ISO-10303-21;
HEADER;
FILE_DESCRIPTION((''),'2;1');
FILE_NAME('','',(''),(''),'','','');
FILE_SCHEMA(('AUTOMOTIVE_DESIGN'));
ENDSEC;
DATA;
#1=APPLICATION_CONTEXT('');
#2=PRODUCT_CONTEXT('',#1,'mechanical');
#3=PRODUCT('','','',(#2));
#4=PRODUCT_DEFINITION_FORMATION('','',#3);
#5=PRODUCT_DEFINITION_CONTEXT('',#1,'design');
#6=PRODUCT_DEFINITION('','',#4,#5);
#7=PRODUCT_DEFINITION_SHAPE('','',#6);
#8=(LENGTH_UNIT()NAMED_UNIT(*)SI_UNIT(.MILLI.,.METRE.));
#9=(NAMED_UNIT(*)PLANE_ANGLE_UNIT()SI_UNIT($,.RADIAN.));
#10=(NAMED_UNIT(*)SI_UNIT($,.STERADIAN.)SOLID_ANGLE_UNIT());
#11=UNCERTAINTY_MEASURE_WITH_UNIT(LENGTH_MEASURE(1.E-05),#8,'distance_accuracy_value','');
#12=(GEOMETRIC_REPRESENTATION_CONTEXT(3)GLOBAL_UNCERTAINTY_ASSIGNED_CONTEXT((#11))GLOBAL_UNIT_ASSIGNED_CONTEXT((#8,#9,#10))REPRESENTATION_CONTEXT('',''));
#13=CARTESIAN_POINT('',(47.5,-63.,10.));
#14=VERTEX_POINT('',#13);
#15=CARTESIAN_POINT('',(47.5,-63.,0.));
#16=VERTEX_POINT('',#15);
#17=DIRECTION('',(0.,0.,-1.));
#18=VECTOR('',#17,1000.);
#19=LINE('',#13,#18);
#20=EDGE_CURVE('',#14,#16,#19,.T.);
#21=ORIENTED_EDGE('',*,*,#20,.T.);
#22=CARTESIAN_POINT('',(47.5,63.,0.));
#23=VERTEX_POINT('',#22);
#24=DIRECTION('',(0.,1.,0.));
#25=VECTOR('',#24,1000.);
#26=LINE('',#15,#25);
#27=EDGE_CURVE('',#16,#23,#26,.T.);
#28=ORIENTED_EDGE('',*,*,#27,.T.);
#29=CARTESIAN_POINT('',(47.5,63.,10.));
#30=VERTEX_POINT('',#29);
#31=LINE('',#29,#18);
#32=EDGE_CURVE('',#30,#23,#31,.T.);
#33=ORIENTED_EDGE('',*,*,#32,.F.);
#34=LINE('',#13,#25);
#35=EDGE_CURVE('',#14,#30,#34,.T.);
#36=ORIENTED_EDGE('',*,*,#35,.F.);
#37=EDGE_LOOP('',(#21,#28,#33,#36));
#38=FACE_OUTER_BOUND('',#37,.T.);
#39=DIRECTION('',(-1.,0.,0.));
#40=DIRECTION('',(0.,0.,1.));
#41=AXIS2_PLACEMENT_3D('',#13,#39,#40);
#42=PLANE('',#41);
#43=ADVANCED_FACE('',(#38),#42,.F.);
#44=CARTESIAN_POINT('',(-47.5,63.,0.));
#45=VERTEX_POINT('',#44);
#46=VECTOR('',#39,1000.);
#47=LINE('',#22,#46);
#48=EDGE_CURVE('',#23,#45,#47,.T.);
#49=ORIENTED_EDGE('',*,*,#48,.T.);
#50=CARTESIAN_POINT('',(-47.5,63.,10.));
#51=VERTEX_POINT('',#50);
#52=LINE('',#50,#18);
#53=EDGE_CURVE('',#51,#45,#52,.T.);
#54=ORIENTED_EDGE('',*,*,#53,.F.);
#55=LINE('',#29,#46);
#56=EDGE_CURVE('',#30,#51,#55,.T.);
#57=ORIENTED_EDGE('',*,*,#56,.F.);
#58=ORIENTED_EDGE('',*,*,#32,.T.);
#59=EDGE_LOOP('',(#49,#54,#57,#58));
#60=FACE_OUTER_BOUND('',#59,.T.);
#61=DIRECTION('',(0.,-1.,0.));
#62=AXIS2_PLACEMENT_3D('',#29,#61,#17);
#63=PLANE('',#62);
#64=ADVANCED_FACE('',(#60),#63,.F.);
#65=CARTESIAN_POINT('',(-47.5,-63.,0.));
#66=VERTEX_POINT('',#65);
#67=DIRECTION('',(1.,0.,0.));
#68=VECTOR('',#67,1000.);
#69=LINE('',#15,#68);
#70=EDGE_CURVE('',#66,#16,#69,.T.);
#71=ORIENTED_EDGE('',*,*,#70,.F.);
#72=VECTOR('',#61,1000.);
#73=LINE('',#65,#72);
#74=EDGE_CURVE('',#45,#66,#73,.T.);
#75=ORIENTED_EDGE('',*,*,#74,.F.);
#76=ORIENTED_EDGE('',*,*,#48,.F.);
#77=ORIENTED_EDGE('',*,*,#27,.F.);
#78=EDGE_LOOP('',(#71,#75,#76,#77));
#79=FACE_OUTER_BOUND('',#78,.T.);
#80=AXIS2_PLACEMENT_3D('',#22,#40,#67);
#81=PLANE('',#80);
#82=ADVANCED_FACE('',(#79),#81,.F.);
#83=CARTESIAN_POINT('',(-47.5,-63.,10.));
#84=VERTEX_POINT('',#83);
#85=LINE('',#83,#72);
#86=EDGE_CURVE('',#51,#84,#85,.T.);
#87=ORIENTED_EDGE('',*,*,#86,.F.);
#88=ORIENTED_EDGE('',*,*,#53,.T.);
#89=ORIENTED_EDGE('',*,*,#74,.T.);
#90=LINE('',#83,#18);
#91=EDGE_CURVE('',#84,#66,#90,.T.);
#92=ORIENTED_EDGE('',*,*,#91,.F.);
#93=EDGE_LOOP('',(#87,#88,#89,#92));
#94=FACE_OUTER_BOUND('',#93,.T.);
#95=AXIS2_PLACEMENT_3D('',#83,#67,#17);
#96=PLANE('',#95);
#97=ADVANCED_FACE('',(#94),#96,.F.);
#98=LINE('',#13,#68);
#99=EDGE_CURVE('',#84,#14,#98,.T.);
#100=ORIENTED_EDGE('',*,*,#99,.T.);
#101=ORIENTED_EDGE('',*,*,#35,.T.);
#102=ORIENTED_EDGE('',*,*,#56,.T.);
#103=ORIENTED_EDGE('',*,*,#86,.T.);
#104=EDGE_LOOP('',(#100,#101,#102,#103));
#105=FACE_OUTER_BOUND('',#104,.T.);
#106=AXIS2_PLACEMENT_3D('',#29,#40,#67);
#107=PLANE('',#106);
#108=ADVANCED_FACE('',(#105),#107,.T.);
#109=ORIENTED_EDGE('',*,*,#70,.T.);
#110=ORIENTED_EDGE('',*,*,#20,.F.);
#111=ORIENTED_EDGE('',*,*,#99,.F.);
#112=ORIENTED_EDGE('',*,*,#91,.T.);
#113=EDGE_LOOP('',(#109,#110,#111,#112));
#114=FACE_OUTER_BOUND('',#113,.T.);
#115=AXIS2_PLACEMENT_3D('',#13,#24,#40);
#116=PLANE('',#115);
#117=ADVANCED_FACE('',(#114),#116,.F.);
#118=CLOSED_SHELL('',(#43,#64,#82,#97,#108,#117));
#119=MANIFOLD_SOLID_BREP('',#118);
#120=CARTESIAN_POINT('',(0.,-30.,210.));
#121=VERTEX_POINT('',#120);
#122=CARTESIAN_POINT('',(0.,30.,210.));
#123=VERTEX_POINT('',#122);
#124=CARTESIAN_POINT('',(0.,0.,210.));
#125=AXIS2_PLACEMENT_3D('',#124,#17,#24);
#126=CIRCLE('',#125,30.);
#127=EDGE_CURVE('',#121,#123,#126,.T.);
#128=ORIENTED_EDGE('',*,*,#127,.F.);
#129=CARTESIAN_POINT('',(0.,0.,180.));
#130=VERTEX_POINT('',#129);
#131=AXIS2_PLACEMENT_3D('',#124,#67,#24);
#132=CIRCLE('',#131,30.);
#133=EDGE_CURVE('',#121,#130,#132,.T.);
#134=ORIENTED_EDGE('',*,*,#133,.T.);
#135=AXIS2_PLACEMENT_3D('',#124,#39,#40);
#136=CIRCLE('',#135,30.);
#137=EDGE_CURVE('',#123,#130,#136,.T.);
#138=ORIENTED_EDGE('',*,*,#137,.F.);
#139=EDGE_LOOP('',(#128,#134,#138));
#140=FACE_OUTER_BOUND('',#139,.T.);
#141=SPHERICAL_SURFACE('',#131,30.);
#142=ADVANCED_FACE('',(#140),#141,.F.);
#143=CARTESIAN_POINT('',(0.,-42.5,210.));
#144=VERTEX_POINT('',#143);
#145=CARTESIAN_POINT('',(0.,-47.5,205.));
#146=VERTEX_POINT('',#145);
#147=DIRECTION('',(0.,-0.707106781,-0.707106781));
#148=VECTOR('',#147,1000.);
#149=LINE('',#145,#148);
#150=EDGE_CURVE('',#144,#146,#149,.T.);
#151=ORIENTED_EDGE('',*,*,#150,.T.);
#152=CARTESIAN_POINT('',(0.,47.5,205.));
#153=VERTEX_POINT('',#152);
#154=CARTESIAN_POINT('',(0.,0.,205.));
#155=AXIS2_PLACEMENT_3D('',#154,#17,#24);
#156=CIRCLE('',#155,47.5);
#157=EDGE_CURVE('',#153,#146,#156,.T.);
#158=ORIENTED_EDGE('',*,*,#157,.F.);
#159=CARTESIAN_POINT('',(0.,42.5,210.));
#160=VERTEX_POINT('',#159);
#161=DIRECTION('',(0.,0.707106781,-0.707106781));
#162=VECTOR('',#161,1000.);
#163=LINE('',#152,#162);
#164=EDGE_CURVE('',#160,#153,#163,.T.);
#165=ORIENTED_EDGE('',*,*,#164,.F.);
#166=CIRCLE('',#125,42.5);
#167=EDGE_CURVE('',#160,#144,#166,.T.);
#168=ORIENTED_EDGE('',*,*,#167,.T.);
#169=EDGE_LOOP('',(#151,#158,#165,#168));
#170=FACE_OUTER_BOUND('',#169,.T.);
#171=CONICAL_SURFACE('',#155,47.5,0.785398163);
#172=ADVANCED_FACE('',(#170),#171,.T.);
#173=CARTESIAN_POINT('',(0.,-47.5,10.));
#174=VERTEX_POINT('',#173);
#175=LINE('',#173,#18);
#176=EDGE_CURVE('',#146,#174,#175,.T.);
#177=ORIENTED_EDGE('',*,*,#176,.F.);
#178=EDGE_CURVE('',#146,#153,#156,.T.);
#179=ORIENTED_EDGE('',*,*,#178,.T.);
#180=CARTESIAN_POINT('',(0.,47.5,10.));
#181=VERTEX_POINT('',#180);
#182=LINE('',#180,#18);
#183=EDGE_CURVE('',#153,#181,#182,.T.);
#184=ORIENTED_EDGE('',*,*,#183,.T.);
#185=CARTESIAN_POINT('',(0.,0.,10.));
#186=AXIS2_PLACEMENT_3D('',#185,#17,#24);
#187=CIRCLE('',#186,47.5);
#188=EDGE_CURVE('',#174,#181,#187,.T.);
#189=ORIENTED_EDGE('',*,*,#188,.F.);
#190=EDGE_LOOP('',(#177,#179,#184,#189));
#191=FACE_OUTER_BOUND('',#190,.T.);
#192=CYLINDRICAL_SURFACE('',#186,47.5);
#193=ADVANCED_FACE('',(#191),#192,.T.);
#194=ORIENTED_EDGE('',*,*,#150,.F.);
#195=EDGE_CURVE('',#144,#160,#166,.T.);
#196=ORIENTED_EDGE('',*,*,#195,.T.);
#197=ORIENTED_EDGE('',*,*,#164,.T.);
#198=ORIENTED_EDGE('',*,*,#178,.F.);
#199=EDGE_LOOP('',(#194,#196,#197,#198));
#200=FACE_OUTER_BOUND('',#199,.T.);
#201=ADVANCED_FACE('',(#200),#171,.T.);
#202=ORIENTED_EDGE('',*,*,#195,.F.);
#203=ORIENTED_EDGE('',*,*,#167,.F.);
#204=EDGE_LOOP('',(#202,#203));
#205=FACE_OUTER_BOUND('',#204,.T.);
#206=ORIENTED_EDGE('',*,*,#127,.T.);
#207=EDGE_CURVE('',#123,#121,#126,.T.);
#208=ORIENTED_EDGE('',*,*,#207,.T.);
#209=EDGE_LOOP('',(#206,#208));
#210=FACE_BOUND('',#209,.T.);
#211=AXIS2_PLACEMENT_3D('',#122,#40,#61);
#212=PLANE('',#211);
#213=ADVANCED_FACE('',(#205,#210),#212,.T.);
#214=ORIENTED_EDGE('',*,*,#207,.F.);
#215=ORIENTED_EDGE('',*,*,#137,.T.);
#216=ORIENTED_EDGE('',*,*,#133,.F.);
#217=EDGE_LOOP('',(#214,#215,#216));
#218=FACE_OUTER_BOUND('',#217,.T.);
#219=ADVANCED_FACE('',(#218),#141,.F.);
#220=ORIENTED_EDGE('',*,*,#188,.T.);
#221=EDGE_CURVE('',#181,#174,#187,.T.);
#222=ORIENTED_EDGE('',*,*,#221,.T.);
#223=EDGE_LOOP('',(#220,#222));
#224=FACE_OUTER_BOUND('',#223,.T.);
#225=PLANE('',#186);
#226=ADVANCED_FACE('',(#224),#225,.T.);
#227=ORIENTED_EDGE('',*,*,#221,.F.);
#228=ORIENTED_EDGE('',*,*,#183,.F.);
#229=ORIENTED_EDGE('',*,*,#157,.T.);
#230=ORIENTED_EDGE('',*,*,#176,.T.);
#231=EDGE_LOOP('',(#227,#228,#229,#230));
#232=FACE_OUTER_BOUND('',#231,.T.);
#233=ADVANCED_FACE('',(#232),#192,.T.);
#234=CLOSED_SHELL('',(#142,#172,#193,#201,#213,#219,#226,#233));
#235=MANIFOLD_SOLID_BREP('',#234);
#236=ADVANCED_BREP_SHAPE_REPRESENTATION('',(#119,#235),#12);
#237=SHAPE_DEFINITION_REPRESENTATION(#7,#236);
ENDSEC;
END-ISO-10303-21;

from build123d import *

# Parameters (mm, degrees)
SKETCH1_W           = 95
SKETCH1_H           = 126
BOSS_EXTRUDE1_DEPTH = 10


with BuildPart() as part:
    # Sketch1 → Boss-Extrude1 (new body)
    with BuildSketch(Plane.XY):
        Rectangle(SKETCH1_W, SKETCH1_H)
    extrude(amount=BOSS_EXTRUDE1_DEPTH)


with BuildPart() as body_2:
    # Sketch3 → Revolve1 (revolve)
    with BuildSketch(Plane(origin=(0, 0, 0), x_dir=(0, 0, -1), z_dir=(1, 0, 0))):
        with BuildLine():
            Line((-10, 0), (-10, 47.5))
            Line((-10, 47.5), (-205, 47.5))
            Line((-205, 47.5), (-210, 42.5))
            Line((-210, 42.5), (-210, 30))
            ThreePointArc((-210, 30), (-188.786796564, 21.213203436), (-180, 0))
            Line((-180, 0), (-10, 0))
        make_face()
    revolve(axis=Axis((0, 0, 10), (0, 0, 1)))


solid = Compound([part.part, body_2.part])
